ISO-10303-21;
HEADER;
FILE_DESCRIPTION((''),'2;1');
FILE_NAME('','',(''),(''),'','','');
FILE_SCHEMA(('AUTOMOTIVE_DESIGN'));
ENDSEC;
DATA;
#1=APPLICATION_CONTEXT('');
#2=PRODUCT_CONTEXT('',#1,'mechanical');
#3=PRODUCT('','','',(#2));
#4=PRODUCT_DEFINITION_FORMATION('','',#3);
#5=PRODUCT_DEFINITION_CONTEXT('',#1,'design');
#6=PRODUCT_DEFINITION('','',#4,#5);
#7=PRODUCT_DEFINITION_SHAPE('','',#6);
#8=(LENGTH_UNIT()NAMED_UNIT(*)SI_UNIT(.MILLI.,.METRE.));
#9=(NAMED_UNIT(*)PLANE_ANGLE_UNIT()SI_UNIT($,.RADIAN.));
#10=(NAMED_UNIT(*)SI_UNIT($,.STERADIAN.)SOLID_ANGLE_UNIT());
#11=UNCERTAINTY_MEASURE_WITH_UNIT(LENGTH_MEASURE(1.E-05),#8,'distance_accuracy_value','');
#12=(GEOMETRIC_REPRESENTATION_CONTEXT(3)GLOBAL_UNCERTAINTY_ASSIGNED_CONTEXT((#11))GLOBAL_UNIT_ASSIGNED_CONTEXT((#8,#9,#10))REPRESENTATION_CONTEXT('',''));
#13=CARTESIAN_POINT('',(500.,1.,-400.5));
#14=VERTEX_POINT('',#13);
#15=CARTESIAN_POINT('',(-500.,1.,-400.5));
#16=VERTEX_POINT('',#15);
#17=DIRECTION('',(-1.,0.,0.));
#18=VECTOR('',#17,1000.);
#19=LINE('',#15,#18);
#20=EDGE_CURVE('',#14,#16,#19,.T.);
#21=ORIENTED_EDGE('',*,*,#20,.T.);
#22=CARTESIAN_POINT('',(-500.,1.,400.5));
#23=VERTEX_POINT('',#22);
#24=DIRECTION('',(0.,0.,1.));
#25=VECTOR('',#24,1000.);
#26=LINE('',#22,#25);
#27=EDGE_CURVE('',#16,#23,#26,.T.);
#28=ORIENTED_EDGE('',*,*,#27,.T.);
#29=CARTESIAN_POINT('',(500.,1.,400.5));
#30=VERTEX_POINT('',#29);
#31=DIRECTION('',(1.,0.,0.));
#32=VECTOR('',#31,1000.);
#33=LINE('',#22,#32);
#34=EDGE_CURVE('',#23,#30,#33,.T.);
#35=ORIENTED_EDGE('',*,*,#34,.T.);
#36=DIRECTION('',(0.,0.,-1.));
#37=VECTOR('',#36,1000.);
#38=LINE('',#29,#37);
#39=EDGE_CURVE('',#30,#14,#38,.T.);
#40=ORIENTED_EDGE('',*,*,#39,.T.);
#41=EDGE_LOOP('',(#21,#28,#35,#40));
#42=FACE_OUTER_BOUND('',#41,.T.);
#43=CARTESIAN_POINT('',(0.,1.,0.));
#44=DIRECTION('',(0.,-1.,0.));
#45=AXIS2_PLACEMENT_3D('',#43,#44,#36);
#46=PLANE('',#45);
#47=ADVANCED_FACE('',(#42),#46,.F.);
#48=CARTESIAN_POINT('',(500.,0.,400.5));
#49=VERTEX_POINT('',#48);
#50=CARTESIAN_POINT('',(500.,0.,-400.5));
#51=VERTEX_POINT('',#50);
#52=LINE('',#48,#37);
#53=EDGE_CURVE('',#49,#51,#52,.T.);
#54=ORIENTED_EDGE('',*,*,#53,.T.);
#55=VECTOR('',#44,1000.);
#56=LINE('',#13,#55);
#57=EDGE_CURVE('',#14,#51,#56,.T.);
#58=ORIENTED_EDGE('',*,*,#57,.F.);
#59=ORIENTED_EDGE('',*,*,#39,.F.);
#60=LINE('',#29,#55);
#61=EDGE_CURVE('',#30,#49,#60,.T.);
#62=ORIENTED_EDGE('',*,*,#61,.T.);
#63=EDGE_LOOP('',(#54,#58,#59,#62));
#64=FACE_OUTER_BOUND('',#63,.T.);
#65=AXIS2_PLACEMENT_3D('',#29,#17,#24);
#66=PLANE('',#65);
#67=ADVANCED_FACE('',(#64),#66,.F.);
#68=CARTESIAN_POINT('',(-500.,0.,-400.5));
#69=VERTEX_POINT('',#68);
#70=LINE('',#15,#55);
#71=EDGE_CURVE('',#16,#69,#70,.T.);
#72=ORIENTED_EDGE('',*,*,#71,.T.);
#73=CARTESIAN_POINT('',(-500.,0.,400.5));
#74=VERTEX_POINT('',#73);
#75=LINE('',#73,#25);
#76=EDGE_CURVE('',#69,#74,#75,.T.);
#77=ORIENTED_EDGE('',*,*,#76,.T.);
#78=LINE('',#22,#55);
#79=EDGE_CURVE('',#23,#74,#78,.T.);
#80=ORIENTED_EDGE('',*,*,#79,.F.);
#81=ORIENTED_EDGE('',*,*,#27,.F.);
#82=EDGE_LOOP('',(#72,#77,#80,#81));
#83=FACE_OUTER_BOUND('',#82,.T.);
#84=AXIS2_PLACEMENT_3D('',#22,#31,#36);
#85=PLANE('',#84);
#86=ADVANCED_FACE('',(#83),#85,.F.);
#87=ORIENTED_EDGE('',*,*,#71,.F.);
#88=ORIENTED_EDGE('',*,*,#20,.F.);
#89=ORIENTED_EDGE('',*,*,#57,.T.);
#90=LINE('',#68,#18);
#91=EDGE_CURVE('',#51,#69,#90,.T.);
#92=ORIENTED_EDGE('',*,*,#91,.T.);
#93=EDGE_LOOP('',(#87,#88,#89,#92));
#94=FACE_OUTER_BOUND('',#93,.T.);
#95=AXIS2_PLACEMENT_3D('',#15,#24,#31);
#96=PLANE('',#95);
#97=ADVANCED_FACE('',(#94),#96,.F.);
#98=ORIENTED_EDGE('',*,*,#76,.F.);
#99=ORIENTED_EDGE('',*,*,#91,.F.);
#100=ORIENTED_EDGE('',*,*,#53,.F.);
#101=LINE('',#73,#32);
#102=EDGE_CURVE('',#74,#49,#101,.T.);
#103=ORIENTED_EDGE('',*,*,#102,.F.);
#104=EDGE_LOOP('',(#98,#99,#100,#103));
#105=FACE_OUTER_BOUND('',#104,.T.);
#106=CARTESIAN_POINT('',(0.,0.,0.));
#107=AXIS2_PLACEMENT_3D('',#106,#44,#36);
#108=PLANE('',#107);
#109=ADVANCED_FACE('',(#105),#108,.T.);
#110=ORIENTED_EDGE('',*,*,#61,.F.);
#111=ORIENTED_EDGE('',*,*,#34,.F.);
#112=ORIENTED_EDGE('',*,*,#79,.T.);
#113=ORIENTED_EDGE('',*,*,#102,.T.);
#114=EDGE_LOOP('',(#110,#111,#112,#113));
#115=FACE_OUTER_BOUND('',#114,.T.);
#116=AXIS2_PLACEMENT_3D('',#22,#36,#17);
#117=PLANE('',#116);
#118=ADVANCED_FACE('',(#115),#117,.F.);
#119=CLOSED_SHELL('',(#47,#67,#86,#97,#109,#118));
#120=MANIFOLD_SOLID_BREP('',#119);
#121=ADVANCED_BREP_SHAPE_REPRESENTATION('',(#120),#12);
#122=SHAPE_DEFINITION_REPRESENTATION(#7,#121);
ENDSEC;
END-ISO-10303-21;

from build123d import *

# Parameters (mm, degrees)
SKETCH1_W           = 1000
SKETCH1_H           = 801
BOSS_EXTRUDE1_DEPTH = 1


with BuildPart() as part:
    # Sketch1 → Boss-Extrude1 (new body)
    with BuildSketch(Plane(origin=(0, 0, 0), x_dir=(1, 0, 0), z_dir=(0, 1, 0))):
        Rectangle(SKETCH1_W, SKETCH1_H)
    extrude(amount=BOSS_EXTRUDE1_DEPTH)


solid = part.part
